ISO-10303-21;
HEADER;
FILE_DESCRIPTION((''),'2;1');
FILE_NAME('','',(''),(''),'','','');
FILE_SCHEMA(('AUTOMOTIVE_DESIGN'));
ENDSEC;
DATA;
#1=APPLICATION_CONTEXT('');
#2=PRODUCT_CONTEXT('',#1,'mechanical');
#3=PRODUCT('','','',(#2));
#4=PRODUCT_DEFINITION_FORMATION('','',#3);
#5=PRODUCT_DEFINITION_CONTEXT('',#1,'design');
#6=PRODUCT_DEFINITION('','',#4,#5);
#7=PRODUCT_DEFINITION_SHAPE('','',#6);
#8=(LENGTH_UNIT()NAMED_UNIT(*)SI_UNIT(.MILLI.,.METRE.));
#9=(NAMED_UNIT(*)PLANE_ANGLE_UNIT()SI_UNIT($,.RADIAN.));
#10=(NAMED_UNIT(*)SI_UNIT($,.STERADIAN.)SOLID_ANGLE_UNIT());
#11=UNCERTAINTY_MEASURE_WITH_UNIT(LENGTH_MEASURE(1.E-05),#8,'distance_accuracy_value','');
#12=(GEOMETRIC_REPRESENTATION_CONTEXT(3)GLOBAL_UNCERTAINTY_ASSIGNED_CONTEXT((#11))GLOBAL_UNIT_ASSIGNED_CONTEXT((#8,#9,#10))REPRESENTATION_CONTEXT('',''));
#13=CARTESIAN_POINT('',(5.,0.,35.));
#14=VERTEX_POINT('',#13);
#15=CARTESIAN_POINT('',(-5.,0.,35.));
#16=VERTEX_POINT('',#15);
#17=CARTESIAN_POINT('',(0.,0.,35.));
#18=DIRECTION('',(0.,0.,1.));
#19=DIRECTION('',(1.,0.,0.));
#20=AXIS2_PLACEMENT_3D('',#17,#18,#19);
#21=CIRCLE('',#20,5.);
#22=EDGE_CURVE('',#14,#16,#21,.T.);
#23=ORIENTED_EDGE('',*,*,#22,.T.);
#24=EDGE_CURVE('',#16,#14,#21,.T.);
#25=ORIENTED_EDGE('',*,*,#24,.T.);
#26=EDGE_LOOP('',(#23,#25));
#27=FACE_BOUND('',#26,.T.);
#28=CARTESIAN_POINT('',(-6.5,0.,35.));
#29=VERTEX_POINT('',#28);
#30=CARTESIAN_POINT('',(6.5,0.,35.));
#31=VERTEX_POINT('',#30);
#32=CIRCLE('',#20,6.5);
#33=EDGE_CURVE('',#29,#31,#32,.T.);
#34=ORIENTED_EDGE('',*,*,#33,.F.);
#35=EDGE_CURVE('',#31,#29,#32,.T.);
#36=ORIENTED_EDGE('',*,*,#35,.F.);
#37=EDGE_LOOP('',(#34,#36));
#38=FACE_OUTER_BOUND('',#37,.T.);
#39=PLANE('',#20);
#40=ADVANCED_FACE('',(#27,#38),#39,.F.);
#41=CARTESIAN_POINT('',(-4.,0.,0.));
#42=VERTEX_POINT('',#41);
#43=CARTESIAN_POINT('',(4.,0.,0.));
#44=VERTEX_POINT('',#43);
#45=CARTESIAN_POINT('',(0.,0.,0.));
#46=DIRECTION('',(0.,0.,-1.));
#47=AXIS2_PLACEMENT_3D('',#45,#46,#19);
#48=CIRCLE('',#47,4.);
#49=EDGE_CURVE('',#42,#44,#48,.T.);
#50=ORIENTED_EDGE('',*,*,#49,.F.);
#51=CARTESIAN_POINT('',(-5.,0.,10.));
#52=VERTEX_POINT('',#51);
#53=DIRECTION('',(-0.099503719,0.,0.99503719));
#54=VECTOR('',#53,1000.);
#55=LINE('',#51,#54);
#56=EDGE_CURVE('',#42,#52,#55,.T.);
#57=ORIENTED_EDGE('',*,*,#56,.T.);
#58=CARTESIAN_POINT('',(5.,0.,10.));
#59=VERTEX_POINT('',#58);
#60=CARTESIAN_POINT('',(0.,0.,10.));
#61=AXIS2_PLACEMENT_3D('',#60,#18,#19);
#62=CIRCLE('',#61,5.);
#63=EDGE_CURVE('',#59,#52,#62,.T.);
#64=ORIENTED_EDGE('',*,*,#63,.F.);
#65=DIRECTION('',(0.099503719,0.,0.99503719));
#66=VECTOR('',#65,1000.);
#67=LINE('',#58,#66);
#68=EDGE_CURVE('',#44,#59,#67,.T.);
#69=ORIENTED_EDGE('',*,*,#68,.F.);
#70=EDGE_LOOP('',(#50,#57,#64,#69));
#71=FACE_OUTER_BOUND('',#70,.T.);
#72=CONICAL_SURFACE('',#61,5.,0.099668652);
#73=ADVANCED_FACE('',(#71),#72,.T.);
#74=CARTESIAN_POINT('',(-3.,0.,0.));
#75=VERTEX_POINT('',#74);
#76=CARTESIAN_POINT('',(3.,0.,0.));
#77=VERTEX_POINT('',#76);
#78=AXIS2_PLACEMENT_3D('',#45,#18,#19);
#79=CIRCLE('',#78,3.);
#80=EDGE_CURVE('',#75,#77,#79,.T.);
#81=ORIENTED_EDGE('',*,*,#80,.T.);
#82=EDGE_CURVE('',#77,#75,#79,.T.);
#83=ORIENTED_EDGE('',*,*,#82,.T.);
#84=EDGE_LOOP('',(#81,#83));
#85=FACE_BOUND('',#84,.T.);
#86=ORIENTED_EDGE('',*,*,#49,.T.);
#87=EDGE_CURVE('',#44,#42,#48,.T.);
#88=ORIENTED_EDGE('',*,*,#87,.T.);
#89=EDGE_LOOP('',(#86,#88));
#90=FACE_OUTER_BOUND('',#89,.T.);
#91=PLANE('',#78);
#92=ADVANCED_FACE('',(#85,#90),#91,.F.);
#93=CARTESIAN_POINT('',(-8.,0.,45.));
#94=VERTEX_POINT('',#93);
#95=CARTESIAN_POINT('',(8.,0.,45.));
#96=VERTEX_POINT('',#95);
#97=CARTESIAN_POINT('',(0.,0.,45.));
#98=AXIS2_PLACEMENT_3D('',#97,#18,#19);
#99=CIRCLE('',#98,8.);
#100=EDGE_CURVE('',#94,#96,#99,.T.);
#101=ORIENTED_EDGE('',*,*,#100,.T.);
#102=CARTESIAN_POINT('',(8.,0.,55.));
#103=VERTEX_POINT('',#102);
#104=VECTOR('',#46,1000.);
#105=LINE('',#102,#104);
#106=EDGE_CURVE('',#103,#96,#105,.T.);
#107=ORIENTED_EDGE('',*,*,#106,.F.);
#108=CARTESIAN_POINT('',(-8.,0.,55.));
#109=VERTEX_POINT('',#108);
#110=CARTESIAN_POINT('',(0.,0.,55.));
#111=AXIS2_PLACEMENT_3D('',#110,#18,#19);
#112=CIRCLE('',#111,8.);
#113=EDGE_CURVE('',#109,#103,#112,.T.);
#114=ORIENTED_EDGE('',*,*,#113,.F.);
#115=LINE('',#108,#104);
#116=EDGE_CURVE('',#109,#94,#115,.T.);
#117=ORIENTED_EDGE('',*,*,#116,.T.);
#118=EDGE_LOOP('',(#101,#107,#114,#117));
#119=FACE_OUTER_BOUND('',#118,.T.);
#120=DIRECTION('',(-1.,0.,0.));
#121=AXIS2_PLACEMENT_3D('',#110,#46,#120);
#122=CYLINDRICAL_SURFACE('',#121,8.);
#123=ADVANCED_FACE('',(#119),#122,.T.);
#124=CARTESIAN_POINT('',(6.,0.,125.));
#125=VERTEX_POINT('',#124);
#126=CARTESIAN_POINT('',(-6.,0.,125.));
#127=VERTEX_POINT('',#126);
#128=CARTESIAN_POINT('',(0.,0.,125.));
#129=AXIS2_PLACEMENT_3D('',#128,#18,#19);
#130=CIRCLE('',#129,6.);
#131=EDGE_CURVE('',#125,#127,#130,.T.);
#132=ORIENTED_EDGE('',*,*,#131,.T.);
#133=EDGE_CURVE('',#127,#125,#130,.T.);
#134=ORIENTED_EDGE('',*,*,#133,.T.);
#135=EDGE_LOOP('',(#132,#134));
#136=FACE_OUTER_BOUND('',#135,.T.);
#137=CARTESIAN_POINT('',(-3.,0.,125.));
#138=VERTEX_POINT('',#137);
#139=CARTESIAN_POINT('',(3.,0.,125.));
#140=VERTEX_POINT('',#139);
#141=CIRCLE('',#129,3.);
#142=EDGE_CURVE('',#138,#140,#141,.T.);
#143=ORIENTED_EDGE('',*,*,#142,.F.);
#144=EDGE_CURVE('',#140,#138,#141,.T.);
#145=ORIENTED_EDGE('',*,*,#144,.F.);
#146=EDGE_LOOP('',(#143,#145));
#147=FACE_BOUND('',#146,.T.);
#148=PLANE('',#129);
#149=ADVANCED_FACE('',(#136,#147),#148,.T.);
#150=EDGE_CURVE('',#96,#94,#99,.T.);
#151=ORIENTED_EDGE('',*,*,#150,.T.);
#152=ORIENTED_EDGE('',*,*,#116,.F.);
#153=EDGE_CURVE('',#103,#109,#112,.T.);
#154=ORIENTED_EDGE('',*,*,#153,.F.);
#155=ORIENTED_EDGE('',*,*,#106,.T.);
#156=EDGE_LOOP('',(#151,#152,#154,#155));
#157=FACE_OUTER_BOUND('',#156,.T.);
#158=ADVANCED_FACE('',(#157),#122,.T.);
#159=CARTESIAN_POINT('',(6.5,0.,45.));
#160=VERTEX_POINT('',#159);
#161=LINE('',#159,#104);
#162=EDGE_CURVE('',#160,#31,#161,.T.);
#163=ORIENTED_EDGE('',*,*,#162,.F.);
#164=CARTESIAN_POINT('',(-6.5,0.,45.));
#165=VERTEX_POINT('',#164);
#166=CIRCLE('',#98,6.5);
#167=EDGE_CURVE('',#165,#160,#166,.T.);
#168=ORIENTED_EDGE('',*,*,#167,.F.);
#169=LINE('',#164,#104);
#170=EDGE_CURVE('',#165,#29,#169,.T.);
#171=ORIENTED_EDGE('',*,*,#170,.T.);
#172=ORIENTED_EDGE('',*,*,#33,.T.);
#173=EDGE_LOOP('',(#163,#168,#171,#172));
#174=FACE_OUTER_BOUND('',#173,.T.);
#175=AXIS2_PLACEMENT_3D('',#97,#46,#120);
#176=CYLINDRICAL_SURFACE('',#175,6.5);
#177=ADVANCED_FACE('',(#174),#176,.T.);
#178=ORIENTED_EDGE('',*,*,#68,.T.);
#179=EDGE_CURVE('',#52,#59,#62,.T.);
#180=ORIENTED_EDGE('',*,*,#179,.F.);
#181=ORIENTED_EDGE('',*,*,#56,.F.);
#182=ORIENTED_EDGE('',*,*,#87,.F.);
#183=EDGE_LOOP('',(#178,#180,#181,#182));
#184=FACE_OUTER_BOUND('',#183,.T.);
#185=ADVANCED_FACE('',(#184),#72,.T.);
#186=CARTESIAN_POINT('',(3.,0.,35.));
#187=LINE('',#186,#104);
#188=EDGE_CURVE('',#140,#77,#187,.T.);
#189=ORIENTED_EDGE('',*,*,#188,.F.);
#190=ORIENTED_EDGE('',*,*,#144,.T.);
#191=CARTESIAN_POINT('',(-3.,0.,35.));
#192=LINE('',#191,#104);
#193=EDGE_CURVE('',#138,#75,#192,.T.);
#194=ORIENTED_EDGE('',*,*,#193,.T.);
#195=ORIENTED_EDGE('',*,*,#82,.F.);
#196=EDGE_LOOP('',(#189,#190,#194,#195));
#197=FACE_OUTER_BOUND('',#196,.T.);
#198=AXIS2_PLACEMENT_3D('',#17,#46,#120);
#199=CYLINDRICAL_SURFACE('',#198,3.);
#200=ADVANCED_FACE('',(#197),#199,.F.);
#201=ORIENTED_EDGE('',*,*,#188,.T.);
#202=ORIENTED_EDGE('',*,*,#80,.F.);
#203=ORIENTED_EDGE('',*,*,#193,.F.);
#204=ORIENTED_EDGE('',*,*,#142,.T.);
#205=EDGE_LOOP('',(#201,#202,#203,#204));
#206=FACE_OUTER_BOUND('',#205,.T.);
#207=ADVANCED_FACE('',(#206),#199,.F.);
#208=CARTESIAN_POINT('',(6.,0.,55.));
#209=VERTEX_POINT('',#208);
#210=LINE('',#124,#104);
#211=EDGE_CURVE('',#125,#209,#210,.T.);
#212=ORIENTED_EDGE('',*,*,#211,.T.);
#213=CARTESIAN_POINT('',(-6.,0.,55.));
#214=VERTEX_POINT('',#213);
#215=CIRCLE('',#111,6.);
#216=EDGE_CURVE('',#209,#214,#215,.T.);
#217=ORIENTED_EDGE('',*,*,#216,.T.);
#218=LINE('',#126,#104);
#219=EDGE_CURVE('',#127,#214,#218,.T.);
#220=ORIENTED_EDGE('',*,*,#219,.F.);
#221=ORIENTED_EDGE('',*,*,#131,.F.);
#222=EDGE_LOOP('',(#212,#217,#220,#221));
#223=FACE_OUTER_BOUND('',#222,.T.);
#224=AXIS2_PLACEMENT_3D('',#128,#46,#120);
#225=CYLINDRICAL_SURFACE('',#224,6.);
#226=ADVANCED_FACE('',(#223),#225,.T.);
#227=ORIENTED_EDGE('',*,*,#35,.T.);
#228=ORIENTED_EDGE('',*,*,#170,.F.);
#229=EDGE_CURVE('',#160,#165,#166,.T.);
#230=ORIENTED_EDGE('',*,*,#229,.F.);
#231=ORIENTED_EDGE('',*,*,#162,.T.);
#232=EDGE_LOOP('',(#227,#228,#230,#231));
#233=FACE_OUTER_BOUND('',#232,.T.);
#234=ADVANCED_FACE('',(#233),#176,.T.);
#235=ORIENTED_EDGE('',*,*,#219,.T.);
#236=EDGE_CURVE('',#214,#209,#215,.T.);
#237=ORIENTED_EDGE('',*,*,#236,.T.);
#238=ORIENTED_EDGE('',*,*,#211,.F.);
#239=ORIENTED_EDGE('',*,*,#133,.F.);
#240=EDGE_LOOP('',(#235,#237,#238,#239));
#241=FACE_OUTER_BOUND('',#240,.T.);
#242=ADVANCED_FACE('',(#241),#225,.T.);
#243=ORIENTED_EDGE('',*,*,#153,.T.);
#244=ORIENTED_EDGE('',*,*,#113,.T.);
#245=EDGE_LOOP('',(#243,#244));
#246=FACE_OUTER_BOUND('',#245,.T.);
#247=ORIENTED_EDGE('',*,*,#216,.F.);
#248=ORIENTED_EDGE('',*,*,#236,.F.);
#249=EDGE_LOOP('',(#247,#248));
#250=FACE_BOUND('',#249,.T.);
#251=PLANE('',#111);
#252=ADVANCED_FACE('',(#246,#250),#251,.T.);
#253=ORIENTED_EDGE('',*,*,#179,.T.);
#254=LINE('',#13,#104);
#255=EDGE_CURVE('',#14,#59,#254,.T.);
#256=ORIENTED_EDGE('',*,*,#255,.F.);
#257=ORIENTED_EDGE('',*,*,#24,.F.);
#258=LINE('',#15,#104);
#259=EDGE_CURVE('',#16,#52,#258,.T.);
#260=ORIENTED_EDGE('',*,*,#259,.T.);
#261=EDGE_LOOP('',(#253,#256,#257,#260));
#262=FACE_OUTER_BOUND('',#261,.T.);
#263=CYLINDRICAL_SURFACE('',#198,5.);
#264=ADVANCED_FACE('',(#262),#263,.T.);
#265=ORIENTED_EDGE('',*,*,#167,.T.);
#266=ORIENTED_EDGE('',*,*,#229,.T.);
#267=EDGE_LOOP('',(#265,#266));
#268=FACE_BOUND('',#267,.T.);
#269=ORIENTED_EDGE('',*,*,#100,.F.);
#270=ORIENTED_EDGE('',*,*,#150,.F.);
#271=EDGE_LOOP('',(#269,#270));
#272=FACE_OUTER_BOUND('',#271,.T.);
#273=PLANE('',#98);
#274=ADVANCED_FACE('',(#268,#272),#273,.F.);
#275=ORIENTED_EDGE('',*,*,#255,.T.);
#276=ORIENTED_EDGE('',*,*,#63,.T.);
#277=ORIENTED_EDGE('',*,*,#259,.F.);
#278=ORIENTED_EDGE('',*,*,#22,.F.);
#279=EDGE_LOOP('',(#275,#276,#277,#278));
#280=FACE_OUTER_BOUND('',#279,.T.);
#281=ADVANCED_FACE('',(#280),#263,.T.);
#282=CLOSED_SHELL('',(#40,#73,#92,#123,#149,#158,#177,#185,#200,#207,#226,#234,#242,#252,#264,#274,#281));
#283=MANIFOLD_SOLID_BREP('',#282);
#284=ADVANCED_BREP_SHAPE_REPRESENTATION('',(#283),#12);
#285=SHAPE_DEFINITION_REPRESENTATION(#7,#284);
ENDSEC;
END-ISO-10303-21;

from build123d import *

# Parameters (mm, degrees)
SKETCH1_R           = 5
SKETCH1_R_2         = 3
BOSS_EXTRUDE1_DEPTH = 35
SKETCH2_R           = 6.5
SKETCH2_R_2         = 3
BOSS_EXTRUDE2_DEPTH = 10
SKETCH3_R           = 8
SKETCH3_R_2         = 3
BOSS_EXTRUDE3_DEPTH = 10
SKETCH4_R           = 6
SKETCH4_R_2         = 3
BOSS_EXTRUDE4_DEPTH = 70
CHAMFER1_SIZE       = 1
CHAMFER1_SIZE2      = 10


with BuildPart() as part:
    # Sketch1 → Boss-Extrude1 (new body)
    with BuildSketch(Plane.XY):
        Circle(SKETCH1_R)
        Circle(SKETCH1_R_2, mode=Mode.SUBTRACT)
    extrude(amount=BOSS_EXTRUDE1_DEPTH)

    # Sketch2 → Boss-Extrude2 (add)
    with BuildSketch(Plane.XY.offset(35)):
        Circle(SKETCH2_R)
        Circle(SKETCH2_R_2, mode=Mode.SUBTRACT)
    extrude(amount=BOSS_EXTRUDE2_DEPTH)

    # Sketch3 → Boss-Extrude3 (add)
    with BuildSketch(Plane.XY.offset(45)):
        Circle(SKETCH3_R)
        Circle(SKETCH3_R_2, mode=Mode.SUBTRACT)
    extrude(amount=BOSS_EXTRUDE3_DEPTH)

    # Sketch4 → Boss-Extrude4 (add)
    with BuildSketch(Plane.XY.offset(55)):
        Circle(SKETCH4_R)
        Circle(SKETCH4_R_2, mode=Mode.SUBTRACT)
    extrude(amount=BOSS_EXTRUDE4_DEPTH)

    # Chamfer1
    chamfer1_edges = [part.edges().sort_by_distance(p)[0] for p in [
        (-5, 0, 0),
    ]]
    chamfer1_side = [part.faces().sort_by_distance(p)[0] for p in [
        (-4.858578644, 0, 0),
    ]]
    chamfer(chamfer1_edges, length=CHAMFER1_SIZE, length2=CHAMFER1_SIZE2, reference=chamfer1_side[0])


solid = part.part
